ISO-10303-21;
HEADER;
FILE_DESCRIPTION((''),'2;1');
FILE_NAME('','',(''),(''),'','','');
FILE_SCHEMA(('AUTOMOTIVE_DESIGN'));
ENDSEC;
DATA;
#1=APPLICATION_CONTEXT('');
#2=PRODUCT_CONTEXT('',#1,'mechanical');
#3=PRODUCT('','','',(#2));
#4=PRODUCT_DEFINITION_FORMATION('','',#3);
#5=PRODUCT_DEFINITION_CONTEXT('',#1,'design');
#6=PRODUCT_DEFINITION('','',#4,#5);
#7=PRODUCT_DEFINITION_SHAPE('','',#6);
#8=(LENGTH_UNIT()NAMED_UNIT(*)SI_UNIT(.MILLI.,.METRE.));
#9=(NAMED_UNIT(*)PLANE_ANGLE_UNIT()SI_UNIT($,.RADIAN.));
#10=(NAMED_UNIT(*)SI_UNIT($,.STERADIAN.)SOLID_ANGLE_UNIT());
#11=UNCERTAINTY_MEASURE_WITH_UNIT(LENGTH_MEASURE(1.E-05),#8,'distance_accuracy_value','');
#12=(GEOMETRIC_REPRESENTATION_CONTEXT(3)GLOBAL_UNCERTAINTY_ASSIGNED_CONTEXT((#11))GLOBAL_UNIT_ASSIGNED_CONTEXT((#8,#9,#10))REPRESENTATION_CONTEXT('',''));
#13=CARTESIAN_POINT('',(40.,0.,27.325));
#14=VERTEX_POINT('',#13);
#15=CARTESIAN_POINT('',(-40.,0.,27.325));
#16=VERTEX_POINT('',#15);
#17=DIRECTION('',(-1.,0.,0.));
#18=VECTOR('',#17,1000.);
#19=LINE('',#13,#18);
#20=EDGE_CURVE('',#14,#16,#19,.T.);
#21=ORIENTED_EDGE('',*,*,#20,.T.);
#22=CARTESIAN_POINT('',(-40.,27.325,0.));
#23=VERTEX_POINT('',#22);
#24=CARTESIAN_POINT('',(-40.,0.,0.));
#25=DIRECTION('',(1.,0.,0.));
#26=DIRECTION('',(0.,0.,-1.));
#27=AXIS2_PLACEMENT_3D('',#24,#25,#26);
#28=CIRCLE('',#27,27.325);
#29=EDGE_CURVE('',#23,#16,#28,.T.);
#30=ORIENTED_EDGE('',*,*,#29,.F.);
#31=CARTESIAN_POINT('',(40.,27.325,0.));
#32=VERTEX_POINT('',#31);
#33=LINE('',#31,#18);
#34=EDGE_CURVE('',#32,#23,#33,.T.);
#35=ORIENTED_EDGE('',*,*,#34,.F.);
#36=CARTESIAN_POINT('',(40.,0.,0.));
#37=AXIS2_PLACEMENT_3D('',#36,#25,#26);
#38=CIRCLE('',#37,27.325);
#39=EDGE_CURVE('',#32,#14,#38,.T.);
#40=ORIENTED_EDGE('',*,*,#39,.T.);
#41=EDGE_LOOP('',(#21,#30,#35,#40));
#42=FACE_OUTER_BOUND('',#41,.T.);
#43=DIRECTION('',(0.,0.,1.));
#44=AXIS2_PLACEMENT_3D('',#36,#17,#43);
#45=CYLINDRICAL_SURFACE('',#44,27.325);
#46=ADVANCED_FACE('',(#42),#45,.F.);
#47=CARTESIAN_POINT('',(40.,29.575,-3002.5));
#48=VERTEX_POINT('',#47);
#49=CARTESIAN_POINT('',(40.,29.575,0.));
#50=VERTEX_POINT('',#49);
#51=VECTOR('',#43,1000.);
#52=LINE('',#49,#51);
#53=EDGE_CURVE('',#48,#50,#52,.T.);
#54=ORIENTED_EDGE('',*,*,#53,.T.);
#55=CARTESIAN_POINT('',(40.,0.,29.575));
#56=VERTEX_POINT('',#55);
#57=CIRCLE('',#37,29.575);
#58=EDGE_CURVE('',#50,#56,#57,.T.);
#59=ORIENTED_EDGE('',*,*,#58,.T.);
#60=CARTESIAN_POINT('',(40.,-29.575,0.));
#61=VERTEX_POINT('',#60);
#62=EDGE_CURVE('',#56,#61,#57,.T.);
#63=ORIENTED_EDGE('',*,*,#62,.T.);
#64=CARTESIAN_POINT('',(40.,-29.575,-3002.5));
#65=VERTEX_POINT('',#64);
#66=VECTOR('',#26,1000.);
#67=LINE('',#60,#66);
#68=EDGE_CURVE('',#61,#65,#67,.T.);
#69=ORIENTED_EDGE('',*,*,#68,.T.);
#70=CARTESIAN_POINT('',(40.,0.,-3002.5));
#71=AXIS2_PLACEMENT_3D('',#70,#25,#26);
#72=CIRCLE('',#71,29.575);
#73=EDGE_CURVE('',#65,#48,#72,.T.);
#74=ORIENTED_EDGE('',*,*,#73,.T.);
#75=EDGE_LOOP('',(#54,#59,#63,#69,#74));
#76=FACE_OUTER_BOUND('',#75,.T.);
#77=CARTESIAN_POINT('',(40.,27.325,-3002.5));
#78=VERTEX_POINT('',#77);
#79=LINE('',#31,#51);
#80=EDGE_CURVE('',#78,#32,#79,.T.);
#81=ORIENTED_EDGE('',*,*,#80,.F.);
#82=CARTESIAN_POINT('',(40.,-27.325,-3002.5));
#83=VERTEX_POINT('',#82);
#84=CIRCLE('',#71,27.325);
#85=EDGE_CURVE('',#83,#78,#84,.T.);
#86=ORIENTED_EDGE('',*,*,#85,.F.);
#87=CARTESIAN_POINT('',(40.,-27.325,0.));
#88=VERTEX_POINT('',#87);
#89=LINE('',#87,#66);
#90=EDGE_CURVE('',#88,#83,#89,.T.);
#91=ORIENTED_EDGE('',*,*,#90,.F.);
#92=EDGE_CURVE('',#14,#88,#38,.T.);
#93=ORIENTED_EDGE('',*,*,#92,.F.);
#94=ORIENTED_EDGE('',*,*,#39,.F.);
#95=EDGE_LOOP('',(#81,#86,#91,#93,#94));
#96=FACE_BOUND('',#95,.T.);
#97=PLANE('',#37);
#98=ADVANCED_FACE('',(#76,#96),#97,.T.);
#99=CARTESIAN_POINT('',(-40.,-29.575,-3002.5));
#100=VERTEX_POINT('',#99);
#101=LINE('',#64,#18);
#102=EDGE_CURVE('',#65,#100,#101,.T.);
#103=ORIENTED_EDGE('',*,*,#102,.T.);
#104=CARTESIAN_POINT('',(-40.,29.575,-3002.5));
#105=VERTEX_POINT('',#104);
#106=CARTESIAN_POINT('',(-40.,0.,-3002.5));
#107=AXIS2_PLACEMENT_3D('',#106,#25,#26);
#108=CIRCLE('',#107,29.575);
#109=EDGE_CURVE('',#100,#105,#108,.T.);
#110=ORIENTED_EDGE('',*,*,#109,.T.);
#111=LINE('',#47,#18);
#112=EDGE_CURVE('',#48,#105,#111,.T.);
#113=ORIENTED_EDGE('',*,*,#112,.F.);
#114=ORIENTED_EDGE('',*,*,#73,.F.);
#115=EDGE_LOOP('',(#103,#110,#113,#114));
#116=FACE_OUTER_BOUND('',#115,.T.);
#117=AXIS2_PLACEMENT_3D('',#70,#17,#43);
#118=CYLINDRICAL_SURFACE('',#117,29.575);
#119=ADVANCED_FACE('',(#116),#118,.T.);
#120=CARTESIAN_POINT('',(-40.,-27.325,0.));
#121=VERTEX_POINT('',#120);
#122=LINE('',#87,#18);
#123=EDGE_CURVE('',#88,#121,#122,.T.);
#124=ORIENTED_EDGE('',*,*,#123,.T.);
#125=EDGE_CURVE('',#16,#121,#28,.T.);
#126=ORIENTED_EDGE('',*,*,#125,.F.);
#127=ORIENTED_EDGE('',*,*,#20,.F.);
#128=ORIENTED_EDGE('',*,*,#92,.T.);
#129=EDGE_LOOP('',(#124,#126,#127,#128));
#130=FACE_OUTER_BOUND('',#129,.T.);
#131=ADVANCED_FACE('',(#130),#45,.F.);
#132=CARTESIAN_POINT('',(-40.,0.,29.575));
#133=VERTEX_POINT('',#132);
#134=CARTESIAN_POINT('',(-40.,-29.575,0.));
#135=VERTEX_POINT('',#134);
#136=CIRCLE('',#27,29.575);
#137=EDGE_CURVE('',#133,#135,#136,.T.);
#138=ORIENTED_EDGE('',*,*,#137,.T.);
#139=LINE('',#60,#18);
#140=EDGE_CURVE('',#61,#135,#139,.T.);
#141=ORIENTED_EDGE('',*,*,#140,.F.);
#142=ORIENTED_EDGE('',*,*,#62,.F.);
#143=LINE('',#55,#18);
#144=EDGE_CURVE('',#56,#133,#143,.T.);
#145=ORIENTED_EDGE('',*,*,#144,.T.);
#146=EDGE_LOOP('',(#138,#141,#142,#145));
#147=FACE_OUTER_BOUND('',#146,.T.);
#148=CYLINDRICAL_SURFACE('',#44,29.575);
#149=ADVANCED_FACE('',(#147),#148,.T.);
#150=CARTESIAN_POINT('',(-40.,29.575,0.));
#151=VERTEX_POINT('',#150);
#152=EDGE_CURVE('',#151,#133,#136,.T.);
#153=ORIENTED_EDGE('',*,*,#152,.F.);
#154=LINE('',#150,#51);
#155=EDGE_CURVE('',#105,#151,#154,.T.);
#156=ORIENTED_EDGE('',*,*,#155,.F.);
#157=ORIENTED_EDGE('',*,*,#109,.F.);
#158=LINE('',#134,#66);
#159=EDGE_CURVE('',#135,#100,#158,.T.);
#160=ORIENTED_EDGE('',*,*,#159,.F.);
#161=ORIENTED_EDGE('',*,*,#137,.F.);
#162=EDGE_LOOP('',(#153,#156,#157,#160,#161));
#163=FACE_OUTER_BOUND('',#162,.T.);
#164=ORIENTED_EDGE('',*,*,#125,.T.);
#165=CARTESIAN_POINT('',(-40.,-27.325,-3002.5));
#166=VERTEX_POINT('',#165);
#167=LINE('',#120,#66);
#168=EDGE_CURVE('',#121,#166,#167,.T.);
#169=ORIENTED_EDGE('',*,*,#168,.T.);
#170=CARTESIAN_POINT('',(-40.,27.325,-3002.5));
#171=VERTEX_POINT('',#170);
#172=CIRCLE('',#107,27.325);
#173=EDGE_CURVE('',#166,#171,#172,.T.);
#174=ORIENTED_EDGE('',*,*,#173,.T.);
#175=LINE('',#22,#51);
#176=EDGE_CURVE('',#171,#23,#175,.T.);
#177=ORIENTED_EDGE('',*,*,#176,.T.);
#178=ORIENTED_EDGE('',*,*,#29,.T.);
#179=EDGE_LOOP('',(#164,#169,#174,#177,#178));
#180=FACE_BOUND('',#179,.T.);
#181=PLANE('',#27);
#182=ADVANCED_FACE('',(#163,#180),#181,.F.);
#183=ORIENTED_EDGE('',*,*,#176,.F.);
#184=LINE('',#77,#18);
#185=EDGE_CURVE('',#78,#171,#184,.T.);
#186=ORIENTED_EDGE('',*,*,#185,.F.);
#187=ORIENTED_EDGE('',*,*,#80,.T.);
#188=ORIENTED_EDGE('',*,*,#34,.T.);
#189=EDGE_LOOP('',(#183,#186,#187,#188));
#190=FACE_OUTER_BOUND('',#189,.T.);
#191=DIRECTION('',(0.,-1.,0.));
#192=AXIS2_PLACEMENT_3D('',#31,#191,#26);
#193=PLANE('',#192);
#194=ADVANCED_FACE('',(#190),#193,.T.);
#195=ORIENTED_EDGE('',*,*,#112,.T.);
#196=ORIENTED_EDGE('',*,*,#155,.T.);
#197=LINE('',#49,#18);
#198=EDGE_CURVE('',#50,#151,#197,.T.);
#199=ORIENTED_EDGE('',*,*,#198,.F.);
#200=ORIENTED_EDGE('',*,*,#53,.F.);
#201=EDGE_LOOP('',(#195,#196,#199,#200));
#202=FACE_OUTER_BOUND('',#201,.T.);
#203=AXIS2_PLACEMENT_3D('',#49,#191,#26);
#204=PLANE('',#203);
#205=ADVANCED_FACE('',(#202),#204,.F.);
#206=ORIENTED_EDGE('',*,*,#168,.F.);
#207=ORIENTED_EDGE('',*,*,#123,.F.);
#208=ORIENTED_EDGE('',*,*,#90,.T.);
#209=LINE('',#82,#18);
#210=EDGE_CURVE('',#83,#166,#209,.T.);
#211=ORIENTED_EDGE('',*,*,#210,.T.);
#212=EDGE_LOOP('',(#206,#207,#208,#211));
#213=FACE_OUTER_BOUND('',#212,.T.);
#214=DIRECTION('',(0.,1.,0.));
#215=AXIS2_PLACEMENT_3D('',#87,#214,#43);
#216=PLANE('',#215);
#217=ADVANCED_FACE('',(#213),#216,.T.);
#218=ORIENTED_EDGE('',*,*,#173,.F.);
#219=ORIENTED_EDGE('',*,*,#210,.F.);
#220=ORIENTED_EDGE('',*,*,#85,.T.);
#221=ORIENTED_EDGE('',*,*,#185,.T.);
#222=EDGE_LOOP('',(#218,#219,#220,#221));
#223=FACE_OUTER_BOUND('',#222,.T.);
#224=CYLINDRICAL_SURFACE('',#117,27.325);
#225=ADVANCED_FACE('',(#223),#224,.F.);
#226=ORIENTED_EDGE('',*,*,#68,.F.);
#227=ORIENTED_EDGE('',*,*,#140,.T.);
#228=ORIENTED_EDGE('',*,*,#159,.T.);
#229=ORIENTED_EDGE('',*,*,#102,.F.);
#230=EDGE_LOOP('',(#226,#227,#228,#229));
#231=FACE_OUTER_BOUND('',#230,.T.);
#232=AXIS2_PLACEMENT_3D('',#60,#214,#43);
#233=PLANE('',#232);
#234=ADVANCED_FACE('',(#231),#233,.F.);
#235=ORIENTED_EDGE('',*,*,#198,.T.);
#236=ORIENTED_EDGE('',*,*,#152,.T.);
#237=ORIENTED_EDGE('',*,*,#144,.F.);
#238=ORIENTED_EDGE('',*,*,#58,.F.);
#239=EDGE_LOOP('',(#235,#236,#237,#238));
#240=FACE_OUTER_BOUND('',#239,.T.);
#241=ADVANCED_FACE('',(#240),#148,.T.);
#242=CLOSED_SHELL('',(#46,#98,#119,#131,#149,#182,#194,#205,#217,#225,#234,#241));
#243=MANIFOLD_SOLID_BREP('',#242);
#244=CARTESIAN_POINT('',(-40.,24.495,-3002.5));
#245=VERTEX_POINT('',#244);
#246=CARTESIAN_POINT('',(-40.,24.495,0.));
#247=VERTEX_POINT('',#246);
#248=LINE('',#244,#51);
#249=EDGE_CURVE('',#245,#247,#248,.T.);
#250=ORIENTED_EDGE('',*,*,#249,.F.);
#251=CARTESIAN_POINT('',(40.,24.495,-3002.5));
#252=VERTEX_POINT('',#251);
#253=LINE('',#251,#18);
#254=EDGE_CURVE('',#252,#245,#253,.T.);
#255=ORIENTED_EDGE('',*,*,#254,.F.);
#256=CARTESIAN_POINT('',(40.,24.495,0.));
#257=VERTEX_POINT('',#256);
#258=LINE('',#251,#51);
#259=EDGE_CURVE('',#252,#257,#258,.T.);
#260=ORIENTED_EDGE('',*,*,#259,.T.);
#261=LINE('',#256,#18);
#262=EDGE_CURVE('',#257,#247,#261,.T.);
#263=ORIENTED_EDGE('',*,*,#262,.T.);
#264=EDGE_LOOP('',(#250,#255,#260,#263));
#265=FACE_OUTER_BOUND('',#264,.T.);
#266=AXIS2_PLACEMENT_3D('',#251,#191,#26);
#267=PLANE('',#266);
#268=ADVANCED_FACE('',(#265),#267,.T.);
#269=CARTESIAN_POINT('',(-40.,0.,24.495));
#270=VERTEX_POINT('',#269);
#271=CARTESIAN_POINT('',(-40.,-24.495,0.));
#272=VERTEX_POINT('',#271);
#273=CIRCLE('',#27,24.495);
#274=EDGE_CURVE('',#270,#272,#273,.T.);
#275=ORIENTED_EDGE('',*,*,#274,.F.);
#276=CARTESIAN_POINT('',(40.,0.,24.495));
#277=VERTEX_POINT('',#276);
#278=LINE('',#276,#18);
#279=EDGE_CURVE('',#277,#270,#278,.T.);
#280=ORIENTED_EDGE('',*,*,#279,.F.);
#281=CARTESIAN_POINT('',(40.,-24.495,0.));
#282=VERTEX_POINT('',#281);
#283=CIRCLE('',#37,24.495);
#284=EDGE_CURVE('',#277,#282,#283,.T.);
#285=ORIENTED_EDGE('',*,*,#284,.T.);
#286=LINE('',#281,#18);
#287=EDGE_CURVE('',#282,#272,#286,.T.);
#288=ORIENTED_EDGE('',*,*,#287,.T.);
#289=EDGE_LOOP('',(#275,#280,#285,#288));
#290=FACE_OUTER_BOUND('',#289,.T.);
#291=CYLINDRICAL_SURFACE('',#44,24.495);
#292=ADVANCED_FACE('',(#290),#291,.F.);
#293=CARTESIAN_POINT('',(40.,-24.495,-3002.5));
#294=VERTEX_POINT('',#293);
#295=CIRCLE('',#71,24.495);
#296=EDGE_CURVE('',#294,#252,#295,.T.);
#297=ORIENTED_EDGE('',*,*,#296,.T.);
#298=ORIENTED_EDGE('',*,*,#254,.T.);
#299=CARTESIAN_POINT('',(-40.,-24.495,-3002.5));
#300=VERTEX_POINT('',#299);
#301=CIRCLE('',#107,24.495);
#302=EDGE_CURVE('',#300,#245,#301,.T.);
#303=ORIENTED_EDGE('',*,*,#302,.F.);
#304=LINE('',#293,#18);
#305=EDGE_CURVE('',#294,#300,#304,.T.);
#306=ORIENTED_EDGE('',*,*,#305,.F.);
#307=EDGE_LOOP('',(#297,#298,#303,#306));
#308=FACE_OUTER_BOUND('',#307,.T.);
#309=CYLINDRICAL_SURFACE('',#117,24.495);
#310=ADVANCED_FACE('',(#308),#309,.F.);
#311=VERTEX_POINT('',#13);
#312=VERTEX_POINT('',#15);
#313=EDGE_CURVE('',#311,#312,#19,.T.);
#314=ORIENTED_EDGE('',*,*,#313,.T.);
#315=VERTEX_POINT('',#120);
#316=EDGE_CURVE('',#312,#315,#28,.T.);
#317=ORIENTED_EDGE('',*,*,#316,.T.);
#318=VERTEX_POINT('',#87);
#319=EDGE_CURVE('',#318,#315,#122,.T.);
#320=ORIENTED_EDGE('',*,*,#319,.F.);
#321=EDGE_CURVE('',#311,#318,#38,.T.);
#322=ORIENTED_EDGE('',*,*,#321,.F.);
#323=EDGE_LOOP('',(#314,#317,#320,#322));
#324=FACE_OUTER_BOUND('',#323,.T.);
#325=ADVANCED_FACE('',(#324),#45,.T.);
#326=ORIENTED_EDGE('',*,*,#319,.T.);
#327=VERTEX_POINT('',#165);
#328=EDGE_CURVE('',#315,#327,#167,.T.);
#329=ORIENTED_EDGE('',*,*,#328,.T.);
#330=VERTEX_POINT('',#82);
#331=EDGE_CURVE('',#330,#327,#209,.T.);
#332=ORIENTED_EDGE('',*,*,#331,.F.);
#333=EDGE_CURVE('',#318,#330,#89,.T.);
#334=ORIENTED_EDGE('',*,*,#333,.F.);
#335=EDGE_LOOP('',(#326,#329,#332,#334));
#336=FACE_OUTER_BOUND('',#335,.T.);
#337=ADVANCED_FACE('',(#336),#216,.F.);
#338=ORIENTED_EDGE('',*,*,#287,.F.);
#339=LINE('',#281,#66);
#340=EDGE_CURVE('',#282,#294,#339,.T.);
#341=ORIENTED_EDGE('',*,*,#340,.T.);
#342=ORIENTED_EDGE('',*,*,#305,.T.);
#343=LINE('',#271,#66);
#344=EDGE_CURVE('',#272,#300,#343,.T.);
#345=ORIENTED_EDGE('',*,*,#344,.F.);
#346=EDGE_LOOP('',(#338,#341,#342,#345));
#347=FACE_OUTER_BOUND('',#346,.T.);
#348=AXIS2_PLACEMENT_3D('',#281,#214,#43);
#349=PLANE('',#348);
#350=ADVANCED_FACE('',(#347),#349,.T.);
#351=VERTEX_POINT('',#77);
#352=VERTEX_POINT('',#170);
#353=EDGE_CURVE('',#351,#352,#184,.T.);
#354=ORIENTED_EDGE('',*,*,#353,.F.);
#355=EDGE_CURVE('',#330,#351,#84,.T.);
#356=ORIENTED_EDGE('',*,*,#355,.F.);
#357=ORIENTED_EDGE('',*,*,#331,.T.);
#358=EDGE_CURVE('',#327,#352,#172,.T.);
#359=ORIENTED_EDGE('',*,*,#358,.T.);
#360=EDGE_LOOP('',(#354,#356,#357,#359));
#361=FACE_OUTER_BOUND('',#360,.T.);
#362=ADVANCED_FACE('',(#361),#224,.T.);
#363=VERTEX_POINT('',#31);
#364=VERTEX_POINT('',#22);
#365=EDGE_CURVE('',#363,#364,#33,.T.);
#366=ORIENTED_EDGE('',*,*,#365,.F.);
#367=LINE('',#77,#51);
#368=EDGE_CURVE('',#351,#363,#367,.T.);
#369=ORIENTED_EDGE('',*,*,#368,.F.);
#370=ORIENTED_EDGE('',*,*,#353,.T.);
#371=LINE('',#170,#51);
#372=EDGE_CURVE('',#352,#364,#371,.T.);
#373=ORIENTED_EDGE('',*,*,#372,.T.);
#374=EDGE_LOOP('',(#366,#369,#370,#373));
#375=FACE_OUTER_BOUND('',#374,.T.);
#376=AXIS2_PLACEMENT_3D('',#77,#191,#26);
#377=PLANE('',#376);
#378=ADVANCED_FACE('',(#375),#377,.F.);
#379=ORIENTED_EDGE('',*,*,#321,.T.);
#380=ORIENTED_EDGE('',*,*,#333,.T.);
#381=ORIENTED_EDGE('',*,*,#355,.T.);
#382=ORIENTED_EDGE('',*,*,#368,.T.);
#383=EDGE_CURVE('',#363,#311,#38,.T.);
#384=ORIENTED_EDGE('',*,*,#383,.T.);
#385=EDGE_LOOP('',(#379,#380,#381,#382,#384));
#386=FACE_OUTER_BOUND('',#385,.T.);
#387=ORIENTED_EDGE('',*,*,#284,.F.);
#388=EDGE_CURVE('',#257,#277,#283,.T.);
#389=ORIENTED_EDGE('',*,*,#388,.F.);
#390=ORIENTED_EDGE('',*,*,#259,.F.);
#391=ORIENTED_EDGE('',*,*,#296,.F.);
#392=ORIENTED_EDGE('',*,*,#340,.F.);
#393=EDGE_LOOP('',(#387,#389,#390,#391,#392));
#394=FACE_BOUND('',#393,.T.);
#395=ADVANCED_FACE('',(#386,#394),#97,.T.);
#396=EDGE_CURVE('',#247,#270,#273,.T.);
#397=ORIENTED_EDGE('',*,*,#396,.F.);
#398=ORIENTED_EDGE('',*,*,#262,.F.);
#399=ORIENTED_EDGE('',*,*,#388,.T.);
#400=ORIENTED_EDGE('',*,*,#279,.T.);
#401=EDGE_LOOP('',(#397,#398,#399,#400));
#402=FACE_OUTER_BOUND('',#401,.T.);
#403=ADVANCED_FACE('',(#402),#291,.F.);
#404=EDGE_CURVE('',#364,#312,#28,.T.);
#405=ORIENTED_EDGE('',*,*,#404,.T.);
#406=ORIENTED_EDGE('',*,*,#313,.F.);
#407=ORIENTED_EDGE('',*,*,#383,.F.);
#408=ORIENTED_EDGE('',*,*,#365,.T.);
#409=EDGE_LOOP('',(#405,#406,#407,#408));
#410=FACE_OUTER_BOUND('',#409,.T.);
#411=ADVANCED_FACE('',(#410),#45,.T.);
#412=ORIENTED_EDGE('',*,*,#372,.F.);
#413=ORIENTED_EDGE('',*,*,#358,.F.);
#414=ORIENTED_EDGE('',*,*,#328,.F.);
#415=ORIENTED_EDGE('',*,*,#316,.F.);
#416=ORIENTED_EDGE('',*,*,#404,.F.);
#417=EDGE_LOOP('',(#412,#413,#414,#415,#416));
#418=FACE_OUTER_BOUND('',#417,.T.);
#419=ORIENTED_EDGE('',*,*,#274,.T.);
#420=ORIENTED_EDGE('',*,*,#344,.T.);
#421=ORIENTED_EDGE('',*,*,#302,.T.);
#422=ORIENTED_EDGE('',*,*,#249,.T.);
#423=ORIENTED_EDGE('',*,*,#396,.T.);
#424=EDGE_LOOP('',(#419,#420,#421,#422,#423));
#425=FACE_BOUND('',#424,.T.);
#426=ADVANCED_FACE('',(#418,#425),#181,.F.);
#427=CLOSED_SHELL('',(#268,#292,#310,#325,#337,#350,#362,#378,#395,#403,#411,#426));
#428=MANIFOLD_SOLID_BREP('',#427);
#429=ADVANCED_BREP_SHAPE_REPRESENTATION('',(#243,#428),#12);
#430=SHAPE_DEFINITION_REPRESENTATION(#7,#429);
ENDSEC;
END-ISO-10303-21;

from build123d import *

# Parameters (mm, degrees)
EXTRUDE_1_DEPTH = 40
EXTRUDE_2_DEPTH = 40


with BuildPart() as part:
    # 草图1 → 拉伸-薄壁1 (new, symmetric)
    with BuildSketch(Plane(origin=(0, 0, 0), x_dir=(0, 0, -1), z_dir=(1, 0, 0))):
        with BuildLine():
            Line((3002.5, -29.575), (0, -29.575))
            ThreePointArc((0, -29.575), (-29.575, 0), (0, 29.575))
            Line((0, 29.575), (3002.5, 29.575))
            ThreePointArc((3002.5, 29.575), (3032.075, 0), (3002.5, -29.575))
        make_face()
        with BuildLine():
            Line((3002.5, -27.325), (0, -27.325))
            ThreePointArc((0, -27.325), (-27.325, 0), (0, 27.325))
            Line((0, 27.325), (3002.5, 27.325))
            ThreePointArc((3002.5, 27.325), (3029.825, 0), (3002.5, -27.325))
        make_face(mode=Mode.SUBTRACT)
    extrude(amount=EXTRUDE_1_DEPTH, both=True)


with BuildPart() as body_2:
    # 草图2 → 拉伸-薄壁2 (new, symmetric)
    with BuildSketch(Plane(origin=(0, 0, 0), x_dir=(0, 0, -1), z_dir=(1, 0, 0))):
        with BuildLine():
            Line((0, -27.325), (3002.5, -27.325))
            ThreePointArc((3002.5, -27.325), (3029.825, 0), (3002.5, 27.325))
            Line((3002.5, 27.325), (0, 27.325))
            ThreePointArc((0, 27.325), (-27.325, 0), (0, -27.325))
        make_face()
        with BuildLine():
            Line((0, -24.495), (3002.5, -24.495))
            ThreePointArc((3002.5, -24.495), (3026.995, 0), (3002.5, 24.495))
            Line((3002.5, 24.495), (0, 24.495))
            ThreePointArc((0, 24.495), (-24.495, 0), (0, -24.495))
        make_face(mode=Mode.SUBTRACT)
    extrude(amount=EXTRUDE_2_DEPTH, both=True)


solid = Compound([part.part, body_2.part])
